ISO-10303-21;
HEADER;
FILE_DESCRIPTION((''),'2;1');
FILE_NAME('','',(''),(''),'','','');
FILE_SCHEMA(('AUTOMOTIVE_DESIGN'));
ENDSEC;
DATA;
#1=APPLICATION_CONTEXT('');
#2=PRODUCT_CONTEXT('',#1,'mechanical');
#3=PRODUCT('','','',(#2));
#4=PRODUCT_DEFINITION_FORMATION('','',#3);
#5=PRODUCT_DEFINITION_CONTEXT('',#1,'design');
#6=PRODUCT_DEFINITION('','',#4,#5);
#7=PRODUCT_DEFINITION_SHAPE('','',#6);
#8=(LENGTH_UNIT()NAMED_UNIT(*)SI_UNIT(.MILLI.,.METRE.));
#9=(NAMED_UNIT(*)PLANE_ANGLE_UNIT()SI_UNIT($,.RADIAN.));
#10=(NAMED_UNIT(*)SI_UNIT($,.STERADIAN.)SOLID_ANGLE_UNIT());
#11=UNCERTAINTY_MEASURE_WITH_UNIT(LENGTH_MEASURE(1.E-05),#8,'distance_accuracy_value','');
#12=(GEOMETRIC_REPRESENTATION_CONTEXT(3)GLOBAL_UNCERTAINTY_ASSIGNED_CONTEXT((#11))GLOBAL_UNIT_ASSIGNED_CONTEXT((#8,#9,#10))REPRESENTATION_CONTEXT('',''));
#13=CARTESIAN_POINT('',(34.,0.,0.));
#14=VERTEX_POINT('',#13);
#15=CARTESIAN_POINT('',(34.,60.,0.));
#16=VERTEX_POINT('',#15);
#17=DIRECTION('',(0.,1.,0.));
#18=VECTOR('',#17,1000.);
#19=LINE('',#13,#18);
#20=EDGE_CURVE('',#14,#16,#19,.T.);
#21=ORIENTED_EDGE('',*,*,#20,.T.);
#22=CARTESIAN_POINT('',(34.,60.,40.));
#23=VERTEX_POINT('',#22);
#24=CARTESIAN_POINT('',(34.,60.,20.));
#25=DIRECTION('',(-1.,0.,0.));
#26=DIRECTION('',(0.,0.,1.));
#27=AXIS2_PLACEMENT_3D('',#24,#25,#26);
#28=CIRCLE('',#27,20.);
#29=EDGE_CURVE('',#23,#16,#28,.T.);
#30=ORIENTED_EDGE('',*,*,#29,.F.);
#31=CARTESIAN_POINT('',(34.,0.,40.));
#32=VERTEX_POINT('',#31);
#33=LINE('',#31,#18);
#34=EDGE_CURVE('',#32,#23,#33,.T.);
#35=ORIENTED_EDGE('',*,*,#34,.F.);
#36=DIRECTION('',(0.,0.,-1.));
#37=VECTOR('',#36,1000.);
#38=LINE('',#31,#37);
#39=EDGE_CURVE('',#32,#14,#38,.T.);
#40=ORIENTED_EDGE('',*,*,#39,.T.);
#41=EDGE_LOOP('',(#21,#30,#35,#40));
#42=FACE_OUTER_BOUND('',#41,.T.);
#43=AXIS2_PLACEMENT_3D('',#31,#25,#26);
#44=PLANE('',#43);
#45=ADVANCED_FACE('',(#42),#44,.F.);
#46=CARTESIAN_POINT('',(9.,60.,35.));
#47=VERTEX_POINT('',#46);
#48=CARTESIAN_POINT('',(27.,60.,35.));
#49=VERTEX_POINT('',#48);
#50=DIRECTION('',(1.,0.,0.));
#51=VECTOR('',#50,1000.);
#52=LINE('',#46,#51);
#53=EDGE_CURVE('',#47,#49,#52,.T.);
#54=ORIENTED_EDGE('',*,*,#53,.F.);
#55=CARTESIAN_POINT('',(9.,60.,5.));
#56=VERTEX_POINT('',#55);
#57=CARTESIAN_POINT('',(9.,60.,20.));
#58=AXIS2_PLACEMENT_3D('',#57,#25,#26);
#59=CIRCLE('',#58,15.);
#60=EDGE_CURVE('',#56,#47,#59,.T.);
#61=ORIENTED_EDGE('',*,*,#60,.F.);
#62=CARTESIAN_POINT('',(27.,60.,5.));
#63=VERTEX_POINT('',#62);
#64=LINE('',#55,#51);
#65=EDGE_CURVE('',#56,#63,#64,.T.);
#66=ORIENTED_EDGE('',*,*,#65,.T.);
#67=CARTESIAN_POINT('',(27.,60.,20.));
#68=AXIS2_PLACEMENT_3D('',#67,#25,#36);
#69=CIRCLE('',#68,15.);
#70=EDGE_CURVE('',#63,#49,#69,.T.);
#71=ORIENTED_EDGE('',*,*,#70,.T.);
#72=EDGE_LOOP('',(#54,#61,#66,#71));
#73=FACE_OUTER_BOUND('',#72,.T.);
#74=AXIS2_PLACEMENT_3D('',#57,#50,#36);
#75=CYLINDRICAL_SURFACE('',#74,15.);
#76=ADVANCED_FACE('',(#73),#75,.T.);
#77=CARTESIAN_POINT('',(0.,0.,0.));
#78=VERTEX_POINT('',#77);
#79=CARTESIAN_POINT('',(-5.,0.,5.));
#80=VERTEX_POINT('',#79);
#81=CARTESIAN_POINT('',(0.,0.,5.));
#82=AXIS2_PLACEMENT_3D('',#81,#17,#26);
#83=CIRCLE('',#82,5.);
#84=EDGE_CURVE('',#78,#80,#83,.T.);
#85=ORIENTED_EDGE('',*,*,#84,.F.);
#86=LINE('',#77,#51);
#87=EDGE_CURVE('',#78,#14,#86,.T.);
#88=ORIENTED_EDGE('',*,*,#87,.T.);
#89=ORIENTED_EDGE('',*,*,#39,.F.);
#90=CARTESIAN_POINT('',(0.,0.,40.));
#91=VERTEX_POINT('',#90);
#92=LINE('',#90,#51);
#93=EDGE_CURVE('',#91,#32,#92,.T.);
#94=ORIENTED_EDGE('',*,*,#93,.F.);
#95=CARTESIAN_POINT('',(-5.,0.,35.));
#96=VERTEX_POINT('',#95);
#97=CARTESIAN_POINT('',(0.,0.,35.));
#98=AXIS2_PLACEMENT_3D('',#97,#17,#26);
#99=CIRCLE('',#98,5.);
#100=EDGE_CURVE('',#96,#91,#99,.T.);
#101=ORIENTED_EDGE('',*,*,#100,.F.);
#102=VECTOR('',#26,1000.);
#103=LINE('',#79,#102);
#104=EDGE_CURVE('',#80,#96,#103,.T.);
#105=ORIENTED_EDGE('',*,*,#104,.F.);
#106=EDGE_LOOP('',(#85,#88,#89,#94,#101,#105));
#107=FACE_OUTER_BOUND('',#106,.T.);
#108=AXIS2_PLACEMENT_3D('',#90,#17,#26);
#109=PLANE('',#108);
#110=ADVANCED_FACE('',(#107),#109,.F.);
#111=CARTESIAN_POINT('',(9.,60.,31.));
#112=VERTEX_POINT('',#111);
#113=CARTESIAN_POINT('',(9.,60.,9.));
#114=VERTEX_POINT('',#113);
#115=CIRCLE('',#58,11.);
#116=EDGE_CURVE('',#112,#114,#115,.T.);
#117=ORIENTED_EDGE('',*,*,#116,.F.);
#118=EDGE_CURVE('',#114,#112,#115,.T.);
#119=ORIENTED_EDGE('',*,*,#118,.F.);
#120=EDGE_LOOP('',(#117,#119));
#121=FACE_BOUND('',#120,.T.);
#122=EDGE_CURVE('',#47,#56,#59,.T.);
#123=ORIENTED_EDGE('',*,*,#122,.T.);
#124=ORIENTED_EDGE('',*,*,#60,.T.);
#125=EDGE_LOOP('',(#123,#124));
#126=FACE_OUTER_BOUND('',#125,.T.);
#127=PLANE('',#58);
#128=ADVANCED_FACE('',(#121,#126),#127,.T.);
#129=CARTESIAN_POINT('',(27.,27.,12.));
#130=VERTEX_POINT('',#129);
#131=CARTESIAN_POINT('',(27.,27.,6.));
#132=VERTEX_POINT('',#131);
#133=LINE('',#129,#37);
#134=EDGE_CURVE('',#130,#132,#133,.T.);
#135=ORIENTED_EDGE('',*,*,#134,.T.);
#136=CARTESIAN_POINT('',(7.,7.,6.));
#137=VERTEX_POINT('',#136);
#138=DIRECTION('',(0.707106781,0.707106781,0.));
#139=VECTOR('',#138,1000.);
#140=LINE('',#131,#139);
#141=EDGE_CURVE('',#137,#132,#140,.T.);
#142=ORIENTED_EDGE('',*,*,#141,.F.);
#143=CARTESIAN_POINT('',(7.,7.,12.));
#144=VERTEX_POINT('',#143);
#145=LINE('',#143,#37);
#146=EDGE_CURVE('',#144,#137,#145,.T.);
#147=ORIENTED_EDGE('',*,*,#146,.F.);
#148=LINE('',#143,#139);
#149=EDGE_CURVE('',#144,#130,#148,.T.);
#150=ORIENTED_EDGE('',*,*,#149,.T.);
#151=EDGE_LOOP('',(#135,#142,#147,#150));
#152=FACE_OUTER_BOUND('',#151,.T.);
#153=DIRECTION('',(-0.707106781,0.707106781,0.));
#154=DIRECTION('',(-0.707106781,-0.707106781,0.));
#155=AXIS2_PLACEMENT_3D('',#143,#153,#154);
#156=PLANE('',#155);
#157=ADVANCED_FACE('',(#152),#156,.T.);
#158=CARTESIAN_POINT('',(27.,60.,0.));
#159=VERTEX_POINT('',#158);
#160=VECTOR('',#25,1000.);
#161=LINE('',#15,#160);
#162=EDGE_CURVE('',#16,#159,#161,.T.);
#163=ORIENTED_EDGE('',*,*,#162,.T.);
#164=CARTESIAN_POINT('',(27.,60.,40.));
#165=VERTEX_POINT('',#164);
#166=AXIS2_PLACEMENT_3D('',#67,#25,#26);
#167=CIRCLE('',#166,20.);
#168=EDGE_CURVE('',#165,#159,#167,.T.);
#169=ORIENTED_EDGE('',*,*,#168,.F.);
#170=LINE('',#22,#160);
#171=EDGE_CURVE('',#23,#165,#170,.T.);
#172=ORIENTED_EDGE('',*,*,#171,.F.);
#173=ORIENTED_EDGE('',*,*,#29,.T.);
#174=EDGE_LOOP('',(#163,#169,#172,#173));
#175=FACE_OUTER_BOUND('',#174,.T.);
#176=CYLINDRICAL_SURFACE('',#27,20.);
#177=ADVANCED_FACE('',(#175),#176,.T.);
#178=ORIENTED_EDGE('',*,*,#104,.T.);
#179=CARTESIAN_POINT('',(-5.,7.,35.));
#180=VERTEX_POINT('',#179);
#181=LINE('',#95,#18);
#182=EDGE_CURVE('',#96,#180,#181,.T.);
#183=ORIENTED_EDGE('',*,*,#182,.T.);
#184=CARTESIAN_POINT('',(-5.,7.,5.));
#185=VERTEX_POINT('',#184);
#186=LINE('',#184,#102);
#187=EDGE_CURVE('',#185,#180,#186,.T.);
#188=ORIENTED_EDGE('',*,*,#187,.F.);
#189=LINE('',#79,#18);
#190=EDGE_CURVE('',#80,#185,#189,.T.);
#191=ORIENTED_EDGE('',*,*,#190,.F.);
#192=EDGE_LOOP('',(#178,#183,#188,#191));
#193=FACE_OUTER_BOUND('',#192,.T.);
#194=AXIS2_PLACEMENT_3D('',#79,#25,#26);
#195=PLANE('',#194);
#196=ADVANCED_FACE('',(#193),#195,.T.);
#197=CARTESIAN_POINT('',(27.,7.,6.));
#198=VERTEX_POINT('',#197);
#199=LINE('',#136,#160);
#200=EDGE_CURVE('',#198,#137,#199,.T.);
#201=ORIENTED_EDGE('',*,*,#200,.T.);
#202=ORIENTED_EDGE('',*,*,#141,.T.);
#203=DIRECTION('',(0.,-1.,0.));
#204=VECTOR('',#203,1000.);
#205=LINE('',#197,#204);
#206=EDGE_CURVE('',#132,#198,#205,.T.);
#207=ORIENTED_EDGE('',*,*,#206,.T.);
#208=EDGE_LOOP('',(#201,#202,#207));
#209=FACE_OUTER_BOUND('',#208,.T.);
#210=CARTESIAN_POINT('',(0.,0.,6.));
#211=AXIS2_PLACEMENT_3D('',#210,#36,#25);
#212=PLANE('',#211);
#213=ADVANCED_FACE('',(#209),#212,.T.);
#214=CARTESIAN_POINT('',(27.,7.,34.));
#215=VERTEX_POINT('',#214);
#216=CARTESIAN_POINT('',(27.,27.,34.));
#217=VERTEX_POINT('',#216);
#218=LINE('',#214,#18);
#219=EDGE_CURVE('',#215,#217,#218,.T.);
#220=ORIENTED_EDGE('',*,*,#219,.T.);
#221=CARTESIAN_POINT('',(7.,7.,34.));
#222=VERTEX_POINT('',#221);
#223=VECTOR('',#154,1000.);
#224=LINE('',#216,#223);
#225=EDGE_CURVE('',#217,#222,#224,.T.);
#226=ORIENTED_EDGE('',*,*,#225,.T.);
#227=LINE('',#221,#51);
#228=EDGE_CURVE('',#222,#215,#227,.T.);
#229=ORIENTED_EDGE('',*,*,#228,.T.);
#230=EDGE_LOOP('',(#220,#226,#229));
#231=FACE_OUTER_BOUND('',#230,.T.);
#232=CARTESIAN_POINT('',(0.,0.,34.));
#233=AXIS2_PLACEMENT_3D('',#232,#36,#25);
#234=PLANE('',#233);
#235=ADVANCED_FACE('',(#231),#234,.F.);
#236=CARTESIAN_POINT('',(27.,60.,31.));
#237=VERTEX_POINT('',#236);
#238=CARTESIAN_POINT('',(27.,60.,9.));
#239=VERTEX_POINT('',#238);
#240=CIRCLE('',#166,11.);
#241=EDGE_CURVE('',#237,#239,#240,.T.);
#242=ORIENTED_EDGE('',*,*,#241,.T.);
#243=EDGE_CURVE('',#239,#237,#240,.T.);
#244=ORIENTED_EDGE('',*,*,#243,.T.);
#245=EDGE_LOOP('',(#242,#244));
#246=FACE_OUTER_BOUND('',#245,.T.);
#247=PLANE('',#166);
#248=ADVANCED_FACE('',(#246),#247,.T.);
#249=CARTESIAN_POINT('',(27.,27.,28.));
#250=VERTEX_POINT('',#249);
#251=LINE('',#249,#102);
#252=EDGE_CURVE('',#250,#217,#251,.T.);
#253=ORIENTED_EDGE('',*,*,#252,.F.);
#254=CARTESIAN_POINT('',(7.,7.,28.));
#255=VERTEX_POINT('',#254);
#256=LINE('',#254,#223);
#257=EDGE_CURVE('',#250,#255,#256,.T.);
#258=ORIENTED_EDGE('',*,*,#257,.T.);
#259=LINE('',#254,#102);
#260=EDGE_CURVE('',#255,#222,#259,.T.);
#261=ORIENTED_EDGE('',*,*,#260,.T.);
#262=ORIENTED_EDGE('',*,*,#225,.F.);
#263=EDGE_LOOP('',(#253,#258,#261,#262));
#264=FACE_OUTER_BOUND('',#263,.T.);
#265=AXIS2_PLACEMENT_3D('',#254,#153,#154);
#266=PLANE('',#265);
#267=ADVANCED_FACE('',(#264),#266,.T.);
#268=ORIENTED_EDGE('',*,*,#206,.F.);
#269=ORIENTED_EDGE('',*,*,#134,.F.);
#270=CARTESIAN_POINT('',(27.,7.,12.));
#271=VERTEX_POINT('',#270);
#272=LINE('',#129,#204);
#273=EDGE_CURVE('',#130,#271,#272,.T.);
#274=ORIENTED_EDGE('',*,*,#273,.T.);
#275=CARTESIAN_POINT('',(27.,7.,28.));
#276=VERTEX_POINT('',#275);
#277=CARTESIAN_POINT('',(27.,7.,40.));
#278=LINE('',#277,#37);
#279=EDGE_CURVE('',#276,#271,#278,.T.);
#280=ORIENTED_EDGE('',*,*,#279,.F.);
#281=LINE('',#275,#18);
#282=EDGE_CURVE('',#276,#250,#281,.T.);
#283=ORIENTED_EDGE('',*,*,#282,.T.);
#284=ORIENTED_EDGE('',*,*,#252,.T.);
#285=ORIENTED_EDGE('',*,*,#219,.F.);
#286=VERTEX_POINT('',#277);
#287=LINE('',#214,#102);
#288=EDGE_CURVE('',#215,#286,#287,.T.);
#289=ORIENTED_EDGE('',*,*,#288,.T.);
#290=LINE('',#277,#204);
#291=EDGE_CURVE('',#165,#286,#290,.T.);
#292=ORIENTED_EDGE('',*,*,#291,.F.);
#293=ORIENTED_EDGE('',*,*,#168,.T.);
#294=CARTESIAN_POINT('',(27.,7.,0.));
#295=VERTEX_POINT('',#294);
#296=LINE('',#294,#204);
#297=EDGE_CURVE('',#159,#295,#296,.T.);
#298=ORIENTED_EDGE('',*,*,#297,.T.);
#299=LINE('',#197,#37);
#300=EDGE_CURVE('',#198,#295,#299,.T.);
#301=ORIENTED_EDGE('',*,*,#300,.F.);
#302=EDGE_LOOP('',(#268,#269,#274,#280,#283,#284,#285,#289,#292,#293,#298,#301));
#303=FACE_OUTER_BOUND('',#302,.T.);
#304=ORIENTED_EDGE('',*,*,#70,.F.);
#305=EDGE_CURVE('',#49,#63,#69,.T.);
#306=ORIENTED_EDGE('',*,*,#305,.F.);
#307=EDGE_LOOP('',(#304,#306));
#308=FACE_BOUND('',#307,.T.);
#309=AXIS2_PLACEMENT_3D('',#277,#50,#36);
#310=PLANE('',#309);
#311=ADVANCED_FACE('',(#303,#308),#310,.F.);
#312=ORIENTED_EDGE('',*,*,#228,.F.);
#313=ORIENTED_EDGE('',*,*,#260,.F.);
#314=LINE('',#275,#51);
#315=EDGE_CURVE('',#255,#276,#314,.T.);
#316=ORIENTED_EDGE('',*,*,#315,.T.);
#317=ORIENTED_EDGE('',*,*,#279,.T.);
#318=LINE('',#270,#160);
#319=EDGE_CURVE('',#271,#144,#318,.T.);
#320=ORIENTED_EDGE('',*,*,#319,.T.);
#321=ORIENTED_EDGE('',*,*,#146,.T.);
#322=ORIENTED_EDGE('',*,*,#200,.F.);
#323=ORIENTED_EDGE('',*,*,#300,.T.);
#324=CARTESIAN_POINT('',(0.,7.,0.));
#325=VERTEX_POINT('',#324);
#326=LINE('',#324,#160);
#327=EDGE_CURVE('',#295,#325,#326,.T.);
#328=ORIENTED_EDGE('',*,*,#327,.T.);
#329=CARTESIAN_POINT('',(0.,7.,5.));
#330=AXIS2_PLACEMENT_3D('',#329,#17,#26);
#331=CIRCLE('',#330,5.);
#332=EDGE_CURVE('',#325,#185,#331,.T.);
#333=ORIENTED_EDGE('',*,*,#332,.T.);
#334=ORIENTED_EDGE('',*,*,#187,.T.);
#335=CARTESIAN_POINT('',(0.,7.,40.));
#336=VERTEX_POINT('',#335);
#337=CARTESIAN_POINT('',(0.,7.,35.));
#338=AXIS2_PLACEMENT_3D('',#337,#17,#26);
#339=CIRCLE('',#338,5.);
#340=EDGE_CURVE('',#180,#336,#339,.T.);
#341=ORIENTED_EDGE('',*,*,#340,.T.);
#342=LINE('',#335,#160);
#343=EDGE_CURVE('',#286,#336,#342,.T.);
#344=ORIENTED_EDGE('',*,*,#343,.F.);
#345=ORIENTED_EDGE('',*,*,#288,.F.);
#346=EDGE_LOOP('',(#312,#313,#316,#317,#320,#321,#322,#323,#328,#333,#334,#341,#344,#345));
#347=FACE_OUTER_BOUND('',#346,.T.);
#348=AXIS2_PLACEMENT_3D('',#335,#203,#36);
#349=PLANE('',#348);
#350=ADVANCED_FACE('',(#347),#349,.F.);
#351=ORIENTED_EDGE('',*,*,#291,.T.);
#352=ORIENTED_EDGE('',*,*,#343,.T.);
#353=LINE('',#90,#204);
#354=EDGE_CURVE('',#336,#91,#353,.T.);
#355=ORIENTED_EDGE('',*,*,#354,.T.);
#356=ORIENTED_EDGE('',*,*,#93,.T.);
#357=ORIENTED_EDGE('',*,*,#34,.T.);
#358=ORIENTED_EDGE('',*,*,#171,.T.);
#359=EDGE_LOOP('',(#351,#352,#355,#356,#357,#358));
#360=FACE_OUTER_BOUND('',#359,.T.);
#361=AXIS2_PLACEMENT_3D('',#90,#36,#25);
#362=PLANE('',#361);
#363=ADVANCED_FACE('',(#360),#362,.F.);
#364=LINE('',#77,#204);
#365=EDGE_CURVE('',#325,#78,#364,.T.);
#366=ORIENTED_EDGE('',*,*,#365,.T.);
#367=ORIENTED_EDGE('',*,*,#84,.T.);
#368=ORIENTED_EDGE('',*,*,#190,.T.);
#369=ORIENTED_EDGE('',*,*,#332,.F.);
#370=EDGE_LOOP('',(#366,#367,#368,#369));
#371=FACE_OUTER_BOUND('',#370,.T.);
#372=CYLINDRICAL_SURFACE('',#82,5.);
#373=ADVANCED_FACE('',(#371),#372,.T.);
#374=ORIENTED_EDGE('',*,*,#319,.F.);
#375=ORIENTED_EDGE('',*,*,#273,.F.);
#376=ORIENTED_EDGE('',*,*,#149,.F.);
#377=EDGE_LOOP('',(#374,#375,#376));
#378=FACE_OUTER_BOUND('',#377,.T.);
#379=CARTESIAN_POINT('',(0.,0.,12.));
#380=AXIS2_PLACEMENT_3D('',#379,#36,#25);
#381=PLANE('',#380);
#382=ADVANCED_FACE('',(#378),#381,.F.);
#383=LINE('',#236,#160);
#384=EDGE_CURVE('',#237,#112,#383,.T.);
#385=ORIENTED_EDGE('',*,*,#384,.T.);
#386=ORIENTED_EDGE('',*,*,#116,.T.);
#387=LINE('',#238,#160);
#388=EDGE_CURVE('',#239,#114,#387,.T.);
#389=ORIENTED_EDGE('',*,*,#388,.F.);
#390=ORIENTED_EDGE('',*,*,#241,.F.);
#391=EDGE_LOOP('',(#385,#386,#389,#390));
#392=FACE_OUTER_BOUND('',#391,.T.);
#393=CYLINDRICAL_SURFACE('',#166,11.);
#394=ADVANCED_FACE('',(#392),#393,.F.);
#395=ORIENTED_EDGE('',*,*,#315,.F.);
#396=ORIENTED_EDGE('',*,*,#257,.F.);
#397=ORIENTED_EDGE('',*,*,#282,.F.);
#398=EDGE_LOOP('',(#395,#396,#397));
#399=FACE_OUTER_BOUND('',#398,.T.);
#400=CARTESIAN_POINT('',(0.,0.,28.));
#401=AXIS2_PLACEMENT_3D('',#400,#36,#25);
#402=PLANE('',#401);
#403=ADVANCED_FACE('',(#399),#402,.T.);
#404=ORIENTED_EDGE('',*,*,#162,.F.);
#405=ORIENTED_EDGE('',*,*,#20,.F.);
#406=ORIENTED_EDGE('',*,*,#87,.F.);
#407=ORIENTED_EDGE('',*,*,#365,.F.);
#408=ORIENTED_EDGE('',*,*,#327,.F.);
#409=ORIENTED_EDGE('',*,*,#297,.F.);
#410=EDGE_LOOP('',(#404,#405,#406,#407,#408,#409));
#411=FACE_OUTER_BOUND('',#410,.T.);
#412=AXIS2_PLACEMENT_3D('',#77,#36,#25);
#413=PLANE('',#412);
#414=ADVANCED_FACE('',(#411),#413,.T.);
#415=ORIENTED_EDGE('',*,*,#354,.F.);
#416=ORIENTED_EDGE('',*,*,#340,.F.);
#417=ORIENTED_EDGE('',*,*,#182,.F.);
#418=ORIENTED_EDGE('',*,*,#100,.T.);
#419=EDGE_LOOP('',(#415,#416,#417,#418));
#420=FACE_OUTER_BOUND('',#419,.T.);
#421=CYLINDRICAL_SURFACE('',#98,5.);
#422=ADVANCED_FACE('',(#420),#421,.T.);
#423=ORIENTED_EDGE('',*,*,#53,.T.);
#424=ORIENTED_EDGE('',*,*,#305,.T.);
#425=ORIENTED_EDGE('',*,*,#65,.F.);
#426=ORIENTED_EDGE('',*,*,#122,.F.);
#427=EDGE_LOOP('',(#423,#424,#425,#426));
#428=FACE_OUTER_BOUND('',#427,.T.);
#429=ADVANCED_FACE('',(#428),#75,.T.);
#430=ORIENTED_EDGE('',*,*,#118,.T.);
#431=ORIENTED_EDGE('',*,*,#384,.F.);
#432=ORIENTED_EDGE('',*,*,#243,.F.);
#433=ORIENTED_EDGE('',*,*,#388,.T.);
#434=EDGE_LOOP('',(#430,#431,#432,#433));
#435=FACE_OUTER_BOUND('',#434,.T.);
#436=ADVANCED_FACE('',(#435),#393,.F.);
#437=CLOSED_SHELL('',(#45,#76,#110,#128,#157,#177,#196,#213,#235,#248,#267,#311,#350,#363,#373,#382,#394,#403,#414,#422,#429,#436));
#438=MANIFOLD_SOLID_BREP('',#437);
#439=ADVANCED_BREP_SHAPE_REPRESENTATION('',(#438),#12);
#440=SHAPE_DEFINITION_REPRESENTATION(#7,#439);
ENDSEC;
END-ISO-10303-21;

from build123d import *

# Parameters (mm, degrees)
L_BRACKET_BASE_DEPTH      = 40
CORNER_BLOCK_DEPTH        = 7
UPRIGHT_ROUNDED_TOP_DEPTH = 7
HUB_SKETCH_30_R           = 15
HUB_30_DEPTH              = 18
BORE_SKETCH_22_R          = 11
BORE_22_DEPTH             = 18
RIB_1_DEPTH               = 12
RIB_2_DEPTH               = 12
TRIANGULAR_CUT_1_DEPTH    = 6
TRIANGULAR_CUT_2_DEPTH    = 6


with BuildPart() as part:
    # L Profile Sketch → L Bracket Base (new body)
    with BuildSketch(Plane.XY):
        Polygon((0, 0), (34, 0), (34, 60), (27, 60), (27, 7), (0, 7), align=None)
    extrude(amount=L_BRACKET_BASE_DEPTH)

    # Corner Block Sketch → Corner Block (add)
    with BuildSketch(Plane(origin=(0, 7, 0), x_dir=(1, 0, 0), z_dir=(0, 1, 0))):
        with BuildLine():
            Line((-5, -5), (-5, -35))
            ThreePointArc((-5, -35), (-3.535533906, -38.535533906), (0, -40))
            Line((0, -40), (0, 0))
            ThreePointArc((0, 0), (-3.535533906, -1.464466094), (-5, -5))
        make_face()
    extrude(amount=-CORNER_BLOCK_DEPTH)

    # Upright Top Arc Sketch → Upright Rounded Top (add)
    with BuildSketch(Plane.ZY.offset(-27)):
        with BuildLine():
            Line((0, 60), (40, 60))
            ThreePointArc((40, 60), (20, 80), (0, 60))
        make_face()
    extrude(amount=-UPRIGHT_ROUNDED_TOP_DEPTH)

    # Hub Sketch Ø30 → Hub Ø30 (add)
    with BuildSketch(Plane.ZY.offset(-27)):
        with Locations(Location((20, 60, 0), (0, 0, 180))):
            Circle(HUB_SKETCH_30_R)
    extrude(amount=HUB_30_DEPTH)

    # Bore Sketch Ø22 → Bore Ø22 (cut)
    with BuildSketch(Plane.ZY.offset(-9)):
        with Locations((20, 60)):
            Circle(BORE_SKETCH_22_R)
    extrude(amount=-BORE_22_DEPTH, mode=Mode.SUBTRACT)

    # Rib 1 Sketch → Rib 1 (add)
    with BuildSketch(Plane.XY.offset(40)):
        Polygon((27, 7), (27, 27), (7, 7), align=None)
    extrude(amount=-RIB_1_DEPTH)

    # Rib 2 Sketch → Rib 2 (add)
    with BuildSketch(Plane(origin=(0, 0, 0), x_dir=(-1, 0, 0), z_dir=(0, 0, -1))):
        Polygon((-27, 7), (-7, 7), (-27, 27), align=None)
    extrude(amount=-RIB_2_DEPTH)

    # Triangular Cut 1 Sketch → Triangular Cut 1 (cut)
    with BuildSketch(Plane(origin=(0, 0, 0), x_dir=(-1, 0, 0), z_dir=(0, 0, -1))):
        Polygon((-27, 27), (-7, 7), (-27, 7), align=None)
    extrude(amount=-TRIANGULAR_CUT_1_DEPTH, mode=Mode.SUBTRACT)

    # Triangular Cut 2 Sketch → Triangular Cut 2 (cut)
    with BuildSketch(Plane.XY.offset(40)):
        Polygon((27, 27), (7, 7), (27, 7), align=None)
    extrude(amount=-TRIANGULAR_CUT_2_DEPTH, mode=Mode.SUBTRACT)


solid = part.part
